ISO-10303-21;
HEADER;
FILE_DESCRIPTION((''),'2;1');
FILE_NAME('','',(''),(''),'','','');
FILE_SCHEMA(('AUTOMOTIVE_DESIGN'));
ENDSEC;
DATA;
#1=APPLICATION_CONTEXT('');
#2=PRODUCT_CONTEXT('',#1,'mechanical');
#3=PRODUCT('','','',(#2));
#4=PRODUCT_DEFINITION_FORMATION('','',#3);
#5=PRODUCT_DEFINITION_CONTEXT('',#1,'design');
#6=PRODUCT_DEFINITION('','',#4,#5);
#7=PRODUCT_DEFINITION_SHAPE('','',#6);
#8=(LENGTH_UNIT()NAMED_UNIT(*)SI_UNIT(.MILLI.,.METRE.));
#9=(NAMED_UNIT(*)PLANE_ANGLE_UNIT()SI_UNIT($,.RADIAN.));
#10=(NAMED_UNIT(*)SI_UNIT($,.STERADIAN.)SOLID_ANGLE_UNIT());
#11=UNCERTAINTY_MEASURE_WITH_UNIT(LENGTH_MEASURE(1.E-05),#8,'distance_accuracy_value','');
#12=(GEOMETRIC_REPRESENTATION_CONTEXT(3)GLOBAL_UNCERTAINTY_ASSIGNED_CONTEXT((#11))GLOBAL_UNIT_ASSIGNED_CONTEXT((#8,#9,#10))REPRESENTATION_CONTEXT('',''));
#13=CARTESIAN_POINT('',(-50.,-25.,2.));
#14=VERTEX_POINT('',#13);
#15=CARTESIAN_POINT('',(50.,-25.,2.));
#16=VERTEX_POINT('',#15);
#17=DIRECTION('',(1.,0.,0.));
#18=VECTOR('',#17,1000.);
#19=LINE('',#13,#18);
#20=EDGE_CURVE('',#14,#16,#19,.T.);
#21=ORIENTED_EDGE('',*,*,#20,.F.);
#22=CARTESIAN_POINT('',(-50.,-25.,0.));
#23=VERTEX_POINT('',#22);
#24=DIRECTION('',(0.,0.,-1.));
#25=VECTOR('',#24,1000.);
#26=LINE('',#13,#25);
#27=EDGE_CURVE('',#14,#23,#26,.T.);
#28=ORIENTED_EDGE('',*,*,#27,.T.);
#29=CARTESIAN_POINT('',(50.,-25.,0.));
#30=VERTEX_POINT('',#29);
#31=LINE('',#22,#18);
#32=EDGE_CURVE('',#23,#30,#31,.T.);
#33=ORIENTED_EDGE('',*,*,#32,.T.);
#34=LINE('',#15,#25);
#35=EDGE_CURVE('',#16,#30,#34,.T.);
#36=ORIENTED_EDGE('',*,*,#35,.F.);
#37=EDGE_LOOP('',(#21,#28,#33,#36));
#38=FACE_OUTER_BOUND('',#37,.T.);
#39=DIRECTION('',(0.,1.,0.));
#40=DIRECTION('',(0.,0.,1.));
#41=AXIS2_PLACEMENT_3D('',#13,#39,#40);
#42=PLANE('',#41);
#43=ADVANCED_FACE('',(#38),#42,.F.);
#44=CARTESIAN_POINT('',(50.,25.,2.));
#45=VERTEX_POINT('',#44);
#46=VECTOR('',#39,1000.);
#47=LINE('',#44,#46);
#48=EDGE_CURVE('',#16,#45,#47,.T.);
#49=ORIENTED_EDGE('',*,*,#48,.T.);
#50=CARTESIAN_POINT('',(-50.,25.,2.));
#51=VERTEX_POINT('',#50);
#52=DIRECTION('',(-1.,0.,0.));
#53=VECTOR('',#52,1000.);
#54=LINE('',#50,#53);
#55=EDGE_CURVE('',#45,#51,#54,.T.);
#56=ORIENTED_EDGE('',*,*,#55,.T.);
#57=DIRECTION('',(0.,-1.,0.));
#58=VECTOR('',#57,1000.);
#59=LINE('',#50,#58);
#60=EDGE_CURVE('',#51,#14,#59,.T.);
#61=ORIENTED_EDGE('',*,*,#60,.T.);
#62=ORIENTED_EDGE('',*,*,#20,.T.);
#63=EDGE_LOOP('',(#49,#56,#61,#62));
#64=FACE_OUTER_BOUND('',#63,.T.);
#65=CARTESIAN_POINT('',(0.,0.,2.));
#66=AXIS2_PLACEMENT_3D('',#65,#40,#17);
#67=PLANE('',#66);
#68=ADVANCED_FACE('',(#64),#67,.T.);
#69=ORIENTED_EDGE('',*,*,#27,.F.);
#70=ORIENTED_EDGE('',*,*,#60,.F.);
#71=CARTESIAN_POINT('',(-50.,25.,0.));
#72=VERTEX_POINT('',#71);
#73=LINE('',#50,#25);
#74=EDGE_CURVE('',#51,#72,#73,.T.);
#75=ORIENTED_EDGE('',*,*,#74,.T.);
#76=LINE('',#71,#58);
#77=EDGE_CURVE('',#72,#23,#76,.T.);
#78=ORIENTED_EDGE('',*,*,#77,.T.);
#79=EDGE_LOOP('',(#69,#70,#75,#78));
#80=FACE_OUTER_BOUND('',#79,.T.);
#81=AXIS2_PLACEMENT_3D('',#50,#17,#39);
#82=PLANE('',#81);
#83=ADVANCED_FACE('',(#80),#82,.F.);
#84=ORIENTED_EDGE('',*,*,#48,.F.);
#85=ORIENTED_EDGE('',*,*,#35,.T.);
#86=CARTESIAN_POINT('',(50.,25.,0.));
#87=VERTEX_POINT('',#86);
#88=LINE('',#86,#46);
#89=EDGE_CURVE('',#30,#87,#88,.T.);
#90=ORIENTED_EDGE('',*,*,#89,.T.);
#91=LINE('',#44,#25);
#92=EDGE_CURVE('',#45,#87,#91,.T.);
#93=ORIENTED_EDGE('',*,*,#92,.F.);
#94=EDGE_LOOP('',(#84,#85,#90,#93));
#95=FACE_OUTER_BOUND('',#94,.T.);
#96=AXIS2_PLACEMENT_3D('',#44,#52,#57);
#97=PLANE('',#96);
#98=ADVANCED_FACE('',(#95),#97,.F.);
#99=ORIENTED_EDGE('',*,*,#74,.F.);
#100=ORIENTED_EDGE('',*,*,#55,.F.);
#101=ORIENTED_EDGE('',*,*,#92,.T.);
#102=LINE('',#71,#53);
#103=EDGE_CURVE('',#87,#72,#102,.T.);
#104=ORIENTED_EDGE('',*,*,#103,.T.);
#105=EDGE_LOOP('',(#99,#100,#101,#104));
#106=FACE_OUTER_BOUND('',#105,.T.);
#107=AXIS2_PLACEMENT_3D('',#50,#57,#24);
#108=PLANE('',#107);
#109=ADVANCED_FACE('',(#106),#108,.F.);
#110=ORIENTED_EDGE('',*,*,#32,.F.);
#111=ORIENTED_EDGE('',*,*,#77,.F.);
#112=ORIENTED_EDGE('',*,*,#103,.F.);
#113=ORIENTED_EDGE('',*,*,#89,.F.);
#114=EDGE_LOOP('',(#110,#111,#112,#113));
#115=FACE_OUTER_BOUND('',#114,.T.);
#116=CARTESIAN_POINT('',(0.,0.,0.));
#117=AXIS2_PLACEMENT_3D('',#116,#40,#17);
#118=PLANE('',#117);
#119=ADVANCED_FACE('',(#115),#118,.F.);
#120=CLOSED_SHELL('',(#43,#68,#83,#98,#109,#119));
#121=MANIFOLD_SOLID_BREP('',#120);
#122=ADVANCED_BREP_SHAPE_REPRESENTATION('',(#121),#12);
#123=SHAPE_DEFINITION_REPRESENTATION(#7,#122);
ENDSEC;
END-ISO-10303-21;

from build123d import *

# Parameters (mm, degrees)
SKETCH1_W           = 100
SKETCH1_H           = 50
BOSS_EXTRUDE1_DEPTH = 2


with BuildPart() as part:
    # Sketch1 → Boss-Extrude1 (new body)
    with BuildSketch(Plane.XY):
        Rectangle(SKETCH1_W, SKETCH1_H)
    extrude(amount=BOSS_EXTRUDE1_DEPTH)


solid = part.part
